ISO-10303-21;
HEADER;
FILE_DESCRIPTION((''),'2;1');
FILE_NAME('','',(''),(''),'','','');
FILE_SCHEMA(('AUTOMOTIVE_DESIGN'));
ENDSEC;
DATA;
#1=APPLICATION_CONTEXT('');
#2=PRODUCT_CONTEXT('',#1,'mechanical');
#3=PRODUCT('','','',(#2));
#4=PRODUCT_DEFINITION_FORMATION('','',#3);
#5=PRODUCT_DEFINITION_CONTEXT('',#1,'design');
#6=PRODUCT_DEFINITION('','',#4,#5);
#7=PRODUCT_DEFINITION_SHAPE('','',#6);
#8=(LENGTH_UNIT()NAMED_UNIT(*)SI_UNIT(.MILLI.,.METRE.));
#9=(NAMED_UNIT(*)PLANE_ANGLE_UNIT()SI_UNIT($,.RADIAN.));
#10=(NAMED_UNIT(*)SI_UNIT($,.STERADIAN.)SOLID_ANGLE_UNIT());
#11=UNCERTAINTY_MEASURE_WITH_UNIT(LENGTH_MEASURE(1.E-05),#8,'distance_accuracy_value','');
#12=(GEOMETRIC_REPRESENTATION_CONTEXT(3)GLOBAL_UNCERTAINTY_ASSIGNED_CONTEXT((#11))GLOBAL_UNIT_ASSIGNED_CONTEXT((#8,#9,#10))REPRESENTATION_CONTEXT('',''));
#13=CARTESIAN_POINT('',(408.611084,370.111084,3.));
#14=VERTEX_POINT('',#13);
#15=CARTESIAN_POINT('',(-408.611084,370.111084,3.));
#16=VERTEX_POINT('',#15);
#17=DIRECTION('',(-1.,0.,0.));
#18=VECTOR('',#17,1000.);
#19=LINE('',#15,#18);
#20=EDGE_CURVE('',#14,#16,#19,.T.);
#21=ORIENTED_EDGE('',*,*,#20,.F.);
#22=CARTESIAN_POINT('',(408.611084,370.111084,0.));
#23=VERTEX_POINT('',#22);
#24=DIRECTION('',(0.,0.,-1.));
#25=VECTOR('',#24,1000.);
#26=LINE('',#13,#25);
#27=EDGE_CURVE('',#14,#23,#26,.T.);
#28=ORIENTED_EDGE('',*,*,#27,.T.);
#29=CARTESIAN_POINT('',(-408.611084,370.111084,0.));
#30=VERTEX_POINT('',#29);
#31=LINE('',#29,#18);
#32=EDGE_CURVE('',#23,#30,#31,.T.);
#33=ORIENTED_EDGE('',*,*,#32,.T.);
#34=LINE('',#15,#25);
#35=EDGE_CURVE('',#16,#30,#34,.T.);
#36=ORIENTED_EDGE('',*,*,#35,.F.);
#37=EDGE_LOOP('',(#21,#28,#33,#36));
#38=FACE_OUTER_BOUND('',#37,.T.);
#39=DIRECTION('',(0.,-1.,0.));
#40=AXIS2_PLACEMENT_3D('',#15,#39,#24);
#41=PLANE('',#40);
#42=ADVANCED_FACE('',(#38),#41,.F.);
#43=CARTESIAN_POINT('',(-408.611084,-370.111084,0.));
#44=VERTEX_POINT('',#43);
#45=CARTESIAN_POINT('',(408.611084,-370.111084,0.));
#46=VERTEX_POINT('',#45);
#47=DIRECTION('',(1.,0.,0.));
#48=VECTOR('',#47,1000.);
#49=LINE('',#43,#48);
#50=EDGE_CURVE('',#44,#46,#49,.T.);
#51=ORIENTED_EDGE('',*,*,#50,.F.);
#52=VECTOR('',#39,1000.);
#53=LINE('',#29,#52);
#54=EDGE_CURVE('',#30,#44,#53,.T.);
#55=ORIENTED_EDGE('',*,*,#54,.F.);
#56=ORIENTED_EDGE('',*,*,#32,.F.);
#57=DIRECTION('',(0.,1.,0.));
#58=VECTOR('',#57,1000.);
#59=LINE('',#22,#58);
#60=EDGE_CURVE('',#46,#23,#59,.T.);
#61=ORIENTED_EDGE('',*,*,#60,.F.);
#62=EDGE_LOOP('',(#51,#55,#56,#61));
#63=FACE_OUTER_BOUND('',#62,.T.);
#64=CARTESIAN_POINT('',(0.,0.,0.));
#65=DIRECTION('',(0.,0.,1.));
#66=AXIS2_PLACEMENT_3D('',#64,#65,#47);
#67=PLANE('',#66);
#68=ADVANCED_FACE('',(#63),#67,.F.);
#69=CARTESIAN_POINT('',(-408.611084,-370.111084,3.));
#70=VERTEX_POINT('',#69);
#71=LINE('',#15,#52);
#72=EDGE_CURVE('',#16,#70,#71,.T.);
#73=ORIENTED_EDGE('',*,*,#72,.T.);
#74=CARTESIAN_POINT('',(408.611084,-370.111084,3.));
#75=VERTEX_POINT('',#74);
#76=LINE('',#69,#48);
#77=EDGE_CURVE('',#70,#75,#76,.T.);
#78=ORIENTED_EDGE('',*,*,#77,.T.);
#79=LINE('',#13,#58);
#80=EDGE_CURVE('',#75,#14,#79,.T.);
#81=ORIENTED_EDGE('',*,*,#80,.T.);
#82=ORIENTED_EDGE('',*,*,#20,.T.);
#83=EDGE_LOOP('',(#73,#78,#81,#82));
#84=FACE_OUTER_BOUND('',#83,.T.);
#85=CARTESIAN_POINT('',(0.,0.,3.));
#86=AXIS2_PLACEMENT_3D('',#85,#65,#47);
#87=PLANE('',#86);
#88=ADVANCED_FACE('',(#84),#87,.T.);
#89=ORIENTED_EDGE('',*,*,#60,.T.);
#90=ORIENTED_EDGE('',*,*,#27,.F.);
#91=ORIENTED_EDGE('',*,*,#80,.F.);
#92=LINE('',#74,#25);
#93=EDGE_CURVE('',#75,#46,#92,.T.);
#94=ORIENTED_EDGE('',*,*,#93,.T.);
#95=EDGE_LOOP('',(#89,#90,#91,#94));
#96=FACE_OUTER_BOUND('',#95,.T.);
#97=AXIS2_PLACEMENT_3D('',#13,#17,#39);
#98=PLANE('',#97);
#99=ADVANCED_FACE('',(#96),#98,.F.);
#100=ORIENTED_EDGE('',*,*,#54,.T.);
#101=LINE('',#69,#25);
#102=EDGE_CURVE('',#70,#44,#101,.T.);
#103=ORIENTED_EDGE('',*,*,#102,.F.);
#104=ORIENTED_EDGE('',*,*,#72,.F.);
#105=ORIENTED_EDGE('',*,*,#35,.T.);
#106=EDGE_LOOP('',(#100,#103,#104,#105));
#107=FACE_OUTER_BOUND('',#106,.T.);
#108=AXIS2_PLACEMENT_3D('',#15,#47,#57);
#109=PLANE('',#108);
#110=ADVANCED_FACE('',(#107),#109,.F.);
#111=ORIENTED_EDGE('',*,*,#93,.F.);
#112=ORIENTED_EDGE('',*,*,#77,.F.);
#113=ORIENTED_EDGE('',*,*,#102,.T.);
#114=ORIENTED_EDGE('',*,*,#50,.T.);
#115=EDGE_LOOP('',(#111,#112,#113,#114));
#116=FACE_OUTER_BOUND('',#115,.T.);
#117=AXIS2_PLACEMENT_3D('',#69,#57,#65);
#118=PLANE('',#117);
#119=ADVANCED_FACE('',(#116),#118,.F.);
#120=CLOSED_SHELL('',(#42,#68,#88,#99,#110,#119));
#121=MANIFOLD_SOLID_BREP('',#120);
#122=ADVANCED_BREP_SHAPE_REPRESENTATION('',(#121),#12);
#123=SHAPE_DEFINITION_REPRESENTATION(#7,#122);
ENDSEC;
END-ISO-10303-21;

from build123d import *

# Parameters (mm, degrees)
SKETCH_1_W      = 817.222167284
SKETCH_1_H      = 740.222167284
EXTRUDE_1_DEPTH = 3


with BuildPart() as part:
    # 草图1 → 凸台-拉伸1 (new body)
    with BuildSketch(Plane.XY):
        Rectangle(SKETCH_1_W, SKETCH_1_H)
    extrude(amount=EXTRUDE_1_DEPTH)


solid = part.part
